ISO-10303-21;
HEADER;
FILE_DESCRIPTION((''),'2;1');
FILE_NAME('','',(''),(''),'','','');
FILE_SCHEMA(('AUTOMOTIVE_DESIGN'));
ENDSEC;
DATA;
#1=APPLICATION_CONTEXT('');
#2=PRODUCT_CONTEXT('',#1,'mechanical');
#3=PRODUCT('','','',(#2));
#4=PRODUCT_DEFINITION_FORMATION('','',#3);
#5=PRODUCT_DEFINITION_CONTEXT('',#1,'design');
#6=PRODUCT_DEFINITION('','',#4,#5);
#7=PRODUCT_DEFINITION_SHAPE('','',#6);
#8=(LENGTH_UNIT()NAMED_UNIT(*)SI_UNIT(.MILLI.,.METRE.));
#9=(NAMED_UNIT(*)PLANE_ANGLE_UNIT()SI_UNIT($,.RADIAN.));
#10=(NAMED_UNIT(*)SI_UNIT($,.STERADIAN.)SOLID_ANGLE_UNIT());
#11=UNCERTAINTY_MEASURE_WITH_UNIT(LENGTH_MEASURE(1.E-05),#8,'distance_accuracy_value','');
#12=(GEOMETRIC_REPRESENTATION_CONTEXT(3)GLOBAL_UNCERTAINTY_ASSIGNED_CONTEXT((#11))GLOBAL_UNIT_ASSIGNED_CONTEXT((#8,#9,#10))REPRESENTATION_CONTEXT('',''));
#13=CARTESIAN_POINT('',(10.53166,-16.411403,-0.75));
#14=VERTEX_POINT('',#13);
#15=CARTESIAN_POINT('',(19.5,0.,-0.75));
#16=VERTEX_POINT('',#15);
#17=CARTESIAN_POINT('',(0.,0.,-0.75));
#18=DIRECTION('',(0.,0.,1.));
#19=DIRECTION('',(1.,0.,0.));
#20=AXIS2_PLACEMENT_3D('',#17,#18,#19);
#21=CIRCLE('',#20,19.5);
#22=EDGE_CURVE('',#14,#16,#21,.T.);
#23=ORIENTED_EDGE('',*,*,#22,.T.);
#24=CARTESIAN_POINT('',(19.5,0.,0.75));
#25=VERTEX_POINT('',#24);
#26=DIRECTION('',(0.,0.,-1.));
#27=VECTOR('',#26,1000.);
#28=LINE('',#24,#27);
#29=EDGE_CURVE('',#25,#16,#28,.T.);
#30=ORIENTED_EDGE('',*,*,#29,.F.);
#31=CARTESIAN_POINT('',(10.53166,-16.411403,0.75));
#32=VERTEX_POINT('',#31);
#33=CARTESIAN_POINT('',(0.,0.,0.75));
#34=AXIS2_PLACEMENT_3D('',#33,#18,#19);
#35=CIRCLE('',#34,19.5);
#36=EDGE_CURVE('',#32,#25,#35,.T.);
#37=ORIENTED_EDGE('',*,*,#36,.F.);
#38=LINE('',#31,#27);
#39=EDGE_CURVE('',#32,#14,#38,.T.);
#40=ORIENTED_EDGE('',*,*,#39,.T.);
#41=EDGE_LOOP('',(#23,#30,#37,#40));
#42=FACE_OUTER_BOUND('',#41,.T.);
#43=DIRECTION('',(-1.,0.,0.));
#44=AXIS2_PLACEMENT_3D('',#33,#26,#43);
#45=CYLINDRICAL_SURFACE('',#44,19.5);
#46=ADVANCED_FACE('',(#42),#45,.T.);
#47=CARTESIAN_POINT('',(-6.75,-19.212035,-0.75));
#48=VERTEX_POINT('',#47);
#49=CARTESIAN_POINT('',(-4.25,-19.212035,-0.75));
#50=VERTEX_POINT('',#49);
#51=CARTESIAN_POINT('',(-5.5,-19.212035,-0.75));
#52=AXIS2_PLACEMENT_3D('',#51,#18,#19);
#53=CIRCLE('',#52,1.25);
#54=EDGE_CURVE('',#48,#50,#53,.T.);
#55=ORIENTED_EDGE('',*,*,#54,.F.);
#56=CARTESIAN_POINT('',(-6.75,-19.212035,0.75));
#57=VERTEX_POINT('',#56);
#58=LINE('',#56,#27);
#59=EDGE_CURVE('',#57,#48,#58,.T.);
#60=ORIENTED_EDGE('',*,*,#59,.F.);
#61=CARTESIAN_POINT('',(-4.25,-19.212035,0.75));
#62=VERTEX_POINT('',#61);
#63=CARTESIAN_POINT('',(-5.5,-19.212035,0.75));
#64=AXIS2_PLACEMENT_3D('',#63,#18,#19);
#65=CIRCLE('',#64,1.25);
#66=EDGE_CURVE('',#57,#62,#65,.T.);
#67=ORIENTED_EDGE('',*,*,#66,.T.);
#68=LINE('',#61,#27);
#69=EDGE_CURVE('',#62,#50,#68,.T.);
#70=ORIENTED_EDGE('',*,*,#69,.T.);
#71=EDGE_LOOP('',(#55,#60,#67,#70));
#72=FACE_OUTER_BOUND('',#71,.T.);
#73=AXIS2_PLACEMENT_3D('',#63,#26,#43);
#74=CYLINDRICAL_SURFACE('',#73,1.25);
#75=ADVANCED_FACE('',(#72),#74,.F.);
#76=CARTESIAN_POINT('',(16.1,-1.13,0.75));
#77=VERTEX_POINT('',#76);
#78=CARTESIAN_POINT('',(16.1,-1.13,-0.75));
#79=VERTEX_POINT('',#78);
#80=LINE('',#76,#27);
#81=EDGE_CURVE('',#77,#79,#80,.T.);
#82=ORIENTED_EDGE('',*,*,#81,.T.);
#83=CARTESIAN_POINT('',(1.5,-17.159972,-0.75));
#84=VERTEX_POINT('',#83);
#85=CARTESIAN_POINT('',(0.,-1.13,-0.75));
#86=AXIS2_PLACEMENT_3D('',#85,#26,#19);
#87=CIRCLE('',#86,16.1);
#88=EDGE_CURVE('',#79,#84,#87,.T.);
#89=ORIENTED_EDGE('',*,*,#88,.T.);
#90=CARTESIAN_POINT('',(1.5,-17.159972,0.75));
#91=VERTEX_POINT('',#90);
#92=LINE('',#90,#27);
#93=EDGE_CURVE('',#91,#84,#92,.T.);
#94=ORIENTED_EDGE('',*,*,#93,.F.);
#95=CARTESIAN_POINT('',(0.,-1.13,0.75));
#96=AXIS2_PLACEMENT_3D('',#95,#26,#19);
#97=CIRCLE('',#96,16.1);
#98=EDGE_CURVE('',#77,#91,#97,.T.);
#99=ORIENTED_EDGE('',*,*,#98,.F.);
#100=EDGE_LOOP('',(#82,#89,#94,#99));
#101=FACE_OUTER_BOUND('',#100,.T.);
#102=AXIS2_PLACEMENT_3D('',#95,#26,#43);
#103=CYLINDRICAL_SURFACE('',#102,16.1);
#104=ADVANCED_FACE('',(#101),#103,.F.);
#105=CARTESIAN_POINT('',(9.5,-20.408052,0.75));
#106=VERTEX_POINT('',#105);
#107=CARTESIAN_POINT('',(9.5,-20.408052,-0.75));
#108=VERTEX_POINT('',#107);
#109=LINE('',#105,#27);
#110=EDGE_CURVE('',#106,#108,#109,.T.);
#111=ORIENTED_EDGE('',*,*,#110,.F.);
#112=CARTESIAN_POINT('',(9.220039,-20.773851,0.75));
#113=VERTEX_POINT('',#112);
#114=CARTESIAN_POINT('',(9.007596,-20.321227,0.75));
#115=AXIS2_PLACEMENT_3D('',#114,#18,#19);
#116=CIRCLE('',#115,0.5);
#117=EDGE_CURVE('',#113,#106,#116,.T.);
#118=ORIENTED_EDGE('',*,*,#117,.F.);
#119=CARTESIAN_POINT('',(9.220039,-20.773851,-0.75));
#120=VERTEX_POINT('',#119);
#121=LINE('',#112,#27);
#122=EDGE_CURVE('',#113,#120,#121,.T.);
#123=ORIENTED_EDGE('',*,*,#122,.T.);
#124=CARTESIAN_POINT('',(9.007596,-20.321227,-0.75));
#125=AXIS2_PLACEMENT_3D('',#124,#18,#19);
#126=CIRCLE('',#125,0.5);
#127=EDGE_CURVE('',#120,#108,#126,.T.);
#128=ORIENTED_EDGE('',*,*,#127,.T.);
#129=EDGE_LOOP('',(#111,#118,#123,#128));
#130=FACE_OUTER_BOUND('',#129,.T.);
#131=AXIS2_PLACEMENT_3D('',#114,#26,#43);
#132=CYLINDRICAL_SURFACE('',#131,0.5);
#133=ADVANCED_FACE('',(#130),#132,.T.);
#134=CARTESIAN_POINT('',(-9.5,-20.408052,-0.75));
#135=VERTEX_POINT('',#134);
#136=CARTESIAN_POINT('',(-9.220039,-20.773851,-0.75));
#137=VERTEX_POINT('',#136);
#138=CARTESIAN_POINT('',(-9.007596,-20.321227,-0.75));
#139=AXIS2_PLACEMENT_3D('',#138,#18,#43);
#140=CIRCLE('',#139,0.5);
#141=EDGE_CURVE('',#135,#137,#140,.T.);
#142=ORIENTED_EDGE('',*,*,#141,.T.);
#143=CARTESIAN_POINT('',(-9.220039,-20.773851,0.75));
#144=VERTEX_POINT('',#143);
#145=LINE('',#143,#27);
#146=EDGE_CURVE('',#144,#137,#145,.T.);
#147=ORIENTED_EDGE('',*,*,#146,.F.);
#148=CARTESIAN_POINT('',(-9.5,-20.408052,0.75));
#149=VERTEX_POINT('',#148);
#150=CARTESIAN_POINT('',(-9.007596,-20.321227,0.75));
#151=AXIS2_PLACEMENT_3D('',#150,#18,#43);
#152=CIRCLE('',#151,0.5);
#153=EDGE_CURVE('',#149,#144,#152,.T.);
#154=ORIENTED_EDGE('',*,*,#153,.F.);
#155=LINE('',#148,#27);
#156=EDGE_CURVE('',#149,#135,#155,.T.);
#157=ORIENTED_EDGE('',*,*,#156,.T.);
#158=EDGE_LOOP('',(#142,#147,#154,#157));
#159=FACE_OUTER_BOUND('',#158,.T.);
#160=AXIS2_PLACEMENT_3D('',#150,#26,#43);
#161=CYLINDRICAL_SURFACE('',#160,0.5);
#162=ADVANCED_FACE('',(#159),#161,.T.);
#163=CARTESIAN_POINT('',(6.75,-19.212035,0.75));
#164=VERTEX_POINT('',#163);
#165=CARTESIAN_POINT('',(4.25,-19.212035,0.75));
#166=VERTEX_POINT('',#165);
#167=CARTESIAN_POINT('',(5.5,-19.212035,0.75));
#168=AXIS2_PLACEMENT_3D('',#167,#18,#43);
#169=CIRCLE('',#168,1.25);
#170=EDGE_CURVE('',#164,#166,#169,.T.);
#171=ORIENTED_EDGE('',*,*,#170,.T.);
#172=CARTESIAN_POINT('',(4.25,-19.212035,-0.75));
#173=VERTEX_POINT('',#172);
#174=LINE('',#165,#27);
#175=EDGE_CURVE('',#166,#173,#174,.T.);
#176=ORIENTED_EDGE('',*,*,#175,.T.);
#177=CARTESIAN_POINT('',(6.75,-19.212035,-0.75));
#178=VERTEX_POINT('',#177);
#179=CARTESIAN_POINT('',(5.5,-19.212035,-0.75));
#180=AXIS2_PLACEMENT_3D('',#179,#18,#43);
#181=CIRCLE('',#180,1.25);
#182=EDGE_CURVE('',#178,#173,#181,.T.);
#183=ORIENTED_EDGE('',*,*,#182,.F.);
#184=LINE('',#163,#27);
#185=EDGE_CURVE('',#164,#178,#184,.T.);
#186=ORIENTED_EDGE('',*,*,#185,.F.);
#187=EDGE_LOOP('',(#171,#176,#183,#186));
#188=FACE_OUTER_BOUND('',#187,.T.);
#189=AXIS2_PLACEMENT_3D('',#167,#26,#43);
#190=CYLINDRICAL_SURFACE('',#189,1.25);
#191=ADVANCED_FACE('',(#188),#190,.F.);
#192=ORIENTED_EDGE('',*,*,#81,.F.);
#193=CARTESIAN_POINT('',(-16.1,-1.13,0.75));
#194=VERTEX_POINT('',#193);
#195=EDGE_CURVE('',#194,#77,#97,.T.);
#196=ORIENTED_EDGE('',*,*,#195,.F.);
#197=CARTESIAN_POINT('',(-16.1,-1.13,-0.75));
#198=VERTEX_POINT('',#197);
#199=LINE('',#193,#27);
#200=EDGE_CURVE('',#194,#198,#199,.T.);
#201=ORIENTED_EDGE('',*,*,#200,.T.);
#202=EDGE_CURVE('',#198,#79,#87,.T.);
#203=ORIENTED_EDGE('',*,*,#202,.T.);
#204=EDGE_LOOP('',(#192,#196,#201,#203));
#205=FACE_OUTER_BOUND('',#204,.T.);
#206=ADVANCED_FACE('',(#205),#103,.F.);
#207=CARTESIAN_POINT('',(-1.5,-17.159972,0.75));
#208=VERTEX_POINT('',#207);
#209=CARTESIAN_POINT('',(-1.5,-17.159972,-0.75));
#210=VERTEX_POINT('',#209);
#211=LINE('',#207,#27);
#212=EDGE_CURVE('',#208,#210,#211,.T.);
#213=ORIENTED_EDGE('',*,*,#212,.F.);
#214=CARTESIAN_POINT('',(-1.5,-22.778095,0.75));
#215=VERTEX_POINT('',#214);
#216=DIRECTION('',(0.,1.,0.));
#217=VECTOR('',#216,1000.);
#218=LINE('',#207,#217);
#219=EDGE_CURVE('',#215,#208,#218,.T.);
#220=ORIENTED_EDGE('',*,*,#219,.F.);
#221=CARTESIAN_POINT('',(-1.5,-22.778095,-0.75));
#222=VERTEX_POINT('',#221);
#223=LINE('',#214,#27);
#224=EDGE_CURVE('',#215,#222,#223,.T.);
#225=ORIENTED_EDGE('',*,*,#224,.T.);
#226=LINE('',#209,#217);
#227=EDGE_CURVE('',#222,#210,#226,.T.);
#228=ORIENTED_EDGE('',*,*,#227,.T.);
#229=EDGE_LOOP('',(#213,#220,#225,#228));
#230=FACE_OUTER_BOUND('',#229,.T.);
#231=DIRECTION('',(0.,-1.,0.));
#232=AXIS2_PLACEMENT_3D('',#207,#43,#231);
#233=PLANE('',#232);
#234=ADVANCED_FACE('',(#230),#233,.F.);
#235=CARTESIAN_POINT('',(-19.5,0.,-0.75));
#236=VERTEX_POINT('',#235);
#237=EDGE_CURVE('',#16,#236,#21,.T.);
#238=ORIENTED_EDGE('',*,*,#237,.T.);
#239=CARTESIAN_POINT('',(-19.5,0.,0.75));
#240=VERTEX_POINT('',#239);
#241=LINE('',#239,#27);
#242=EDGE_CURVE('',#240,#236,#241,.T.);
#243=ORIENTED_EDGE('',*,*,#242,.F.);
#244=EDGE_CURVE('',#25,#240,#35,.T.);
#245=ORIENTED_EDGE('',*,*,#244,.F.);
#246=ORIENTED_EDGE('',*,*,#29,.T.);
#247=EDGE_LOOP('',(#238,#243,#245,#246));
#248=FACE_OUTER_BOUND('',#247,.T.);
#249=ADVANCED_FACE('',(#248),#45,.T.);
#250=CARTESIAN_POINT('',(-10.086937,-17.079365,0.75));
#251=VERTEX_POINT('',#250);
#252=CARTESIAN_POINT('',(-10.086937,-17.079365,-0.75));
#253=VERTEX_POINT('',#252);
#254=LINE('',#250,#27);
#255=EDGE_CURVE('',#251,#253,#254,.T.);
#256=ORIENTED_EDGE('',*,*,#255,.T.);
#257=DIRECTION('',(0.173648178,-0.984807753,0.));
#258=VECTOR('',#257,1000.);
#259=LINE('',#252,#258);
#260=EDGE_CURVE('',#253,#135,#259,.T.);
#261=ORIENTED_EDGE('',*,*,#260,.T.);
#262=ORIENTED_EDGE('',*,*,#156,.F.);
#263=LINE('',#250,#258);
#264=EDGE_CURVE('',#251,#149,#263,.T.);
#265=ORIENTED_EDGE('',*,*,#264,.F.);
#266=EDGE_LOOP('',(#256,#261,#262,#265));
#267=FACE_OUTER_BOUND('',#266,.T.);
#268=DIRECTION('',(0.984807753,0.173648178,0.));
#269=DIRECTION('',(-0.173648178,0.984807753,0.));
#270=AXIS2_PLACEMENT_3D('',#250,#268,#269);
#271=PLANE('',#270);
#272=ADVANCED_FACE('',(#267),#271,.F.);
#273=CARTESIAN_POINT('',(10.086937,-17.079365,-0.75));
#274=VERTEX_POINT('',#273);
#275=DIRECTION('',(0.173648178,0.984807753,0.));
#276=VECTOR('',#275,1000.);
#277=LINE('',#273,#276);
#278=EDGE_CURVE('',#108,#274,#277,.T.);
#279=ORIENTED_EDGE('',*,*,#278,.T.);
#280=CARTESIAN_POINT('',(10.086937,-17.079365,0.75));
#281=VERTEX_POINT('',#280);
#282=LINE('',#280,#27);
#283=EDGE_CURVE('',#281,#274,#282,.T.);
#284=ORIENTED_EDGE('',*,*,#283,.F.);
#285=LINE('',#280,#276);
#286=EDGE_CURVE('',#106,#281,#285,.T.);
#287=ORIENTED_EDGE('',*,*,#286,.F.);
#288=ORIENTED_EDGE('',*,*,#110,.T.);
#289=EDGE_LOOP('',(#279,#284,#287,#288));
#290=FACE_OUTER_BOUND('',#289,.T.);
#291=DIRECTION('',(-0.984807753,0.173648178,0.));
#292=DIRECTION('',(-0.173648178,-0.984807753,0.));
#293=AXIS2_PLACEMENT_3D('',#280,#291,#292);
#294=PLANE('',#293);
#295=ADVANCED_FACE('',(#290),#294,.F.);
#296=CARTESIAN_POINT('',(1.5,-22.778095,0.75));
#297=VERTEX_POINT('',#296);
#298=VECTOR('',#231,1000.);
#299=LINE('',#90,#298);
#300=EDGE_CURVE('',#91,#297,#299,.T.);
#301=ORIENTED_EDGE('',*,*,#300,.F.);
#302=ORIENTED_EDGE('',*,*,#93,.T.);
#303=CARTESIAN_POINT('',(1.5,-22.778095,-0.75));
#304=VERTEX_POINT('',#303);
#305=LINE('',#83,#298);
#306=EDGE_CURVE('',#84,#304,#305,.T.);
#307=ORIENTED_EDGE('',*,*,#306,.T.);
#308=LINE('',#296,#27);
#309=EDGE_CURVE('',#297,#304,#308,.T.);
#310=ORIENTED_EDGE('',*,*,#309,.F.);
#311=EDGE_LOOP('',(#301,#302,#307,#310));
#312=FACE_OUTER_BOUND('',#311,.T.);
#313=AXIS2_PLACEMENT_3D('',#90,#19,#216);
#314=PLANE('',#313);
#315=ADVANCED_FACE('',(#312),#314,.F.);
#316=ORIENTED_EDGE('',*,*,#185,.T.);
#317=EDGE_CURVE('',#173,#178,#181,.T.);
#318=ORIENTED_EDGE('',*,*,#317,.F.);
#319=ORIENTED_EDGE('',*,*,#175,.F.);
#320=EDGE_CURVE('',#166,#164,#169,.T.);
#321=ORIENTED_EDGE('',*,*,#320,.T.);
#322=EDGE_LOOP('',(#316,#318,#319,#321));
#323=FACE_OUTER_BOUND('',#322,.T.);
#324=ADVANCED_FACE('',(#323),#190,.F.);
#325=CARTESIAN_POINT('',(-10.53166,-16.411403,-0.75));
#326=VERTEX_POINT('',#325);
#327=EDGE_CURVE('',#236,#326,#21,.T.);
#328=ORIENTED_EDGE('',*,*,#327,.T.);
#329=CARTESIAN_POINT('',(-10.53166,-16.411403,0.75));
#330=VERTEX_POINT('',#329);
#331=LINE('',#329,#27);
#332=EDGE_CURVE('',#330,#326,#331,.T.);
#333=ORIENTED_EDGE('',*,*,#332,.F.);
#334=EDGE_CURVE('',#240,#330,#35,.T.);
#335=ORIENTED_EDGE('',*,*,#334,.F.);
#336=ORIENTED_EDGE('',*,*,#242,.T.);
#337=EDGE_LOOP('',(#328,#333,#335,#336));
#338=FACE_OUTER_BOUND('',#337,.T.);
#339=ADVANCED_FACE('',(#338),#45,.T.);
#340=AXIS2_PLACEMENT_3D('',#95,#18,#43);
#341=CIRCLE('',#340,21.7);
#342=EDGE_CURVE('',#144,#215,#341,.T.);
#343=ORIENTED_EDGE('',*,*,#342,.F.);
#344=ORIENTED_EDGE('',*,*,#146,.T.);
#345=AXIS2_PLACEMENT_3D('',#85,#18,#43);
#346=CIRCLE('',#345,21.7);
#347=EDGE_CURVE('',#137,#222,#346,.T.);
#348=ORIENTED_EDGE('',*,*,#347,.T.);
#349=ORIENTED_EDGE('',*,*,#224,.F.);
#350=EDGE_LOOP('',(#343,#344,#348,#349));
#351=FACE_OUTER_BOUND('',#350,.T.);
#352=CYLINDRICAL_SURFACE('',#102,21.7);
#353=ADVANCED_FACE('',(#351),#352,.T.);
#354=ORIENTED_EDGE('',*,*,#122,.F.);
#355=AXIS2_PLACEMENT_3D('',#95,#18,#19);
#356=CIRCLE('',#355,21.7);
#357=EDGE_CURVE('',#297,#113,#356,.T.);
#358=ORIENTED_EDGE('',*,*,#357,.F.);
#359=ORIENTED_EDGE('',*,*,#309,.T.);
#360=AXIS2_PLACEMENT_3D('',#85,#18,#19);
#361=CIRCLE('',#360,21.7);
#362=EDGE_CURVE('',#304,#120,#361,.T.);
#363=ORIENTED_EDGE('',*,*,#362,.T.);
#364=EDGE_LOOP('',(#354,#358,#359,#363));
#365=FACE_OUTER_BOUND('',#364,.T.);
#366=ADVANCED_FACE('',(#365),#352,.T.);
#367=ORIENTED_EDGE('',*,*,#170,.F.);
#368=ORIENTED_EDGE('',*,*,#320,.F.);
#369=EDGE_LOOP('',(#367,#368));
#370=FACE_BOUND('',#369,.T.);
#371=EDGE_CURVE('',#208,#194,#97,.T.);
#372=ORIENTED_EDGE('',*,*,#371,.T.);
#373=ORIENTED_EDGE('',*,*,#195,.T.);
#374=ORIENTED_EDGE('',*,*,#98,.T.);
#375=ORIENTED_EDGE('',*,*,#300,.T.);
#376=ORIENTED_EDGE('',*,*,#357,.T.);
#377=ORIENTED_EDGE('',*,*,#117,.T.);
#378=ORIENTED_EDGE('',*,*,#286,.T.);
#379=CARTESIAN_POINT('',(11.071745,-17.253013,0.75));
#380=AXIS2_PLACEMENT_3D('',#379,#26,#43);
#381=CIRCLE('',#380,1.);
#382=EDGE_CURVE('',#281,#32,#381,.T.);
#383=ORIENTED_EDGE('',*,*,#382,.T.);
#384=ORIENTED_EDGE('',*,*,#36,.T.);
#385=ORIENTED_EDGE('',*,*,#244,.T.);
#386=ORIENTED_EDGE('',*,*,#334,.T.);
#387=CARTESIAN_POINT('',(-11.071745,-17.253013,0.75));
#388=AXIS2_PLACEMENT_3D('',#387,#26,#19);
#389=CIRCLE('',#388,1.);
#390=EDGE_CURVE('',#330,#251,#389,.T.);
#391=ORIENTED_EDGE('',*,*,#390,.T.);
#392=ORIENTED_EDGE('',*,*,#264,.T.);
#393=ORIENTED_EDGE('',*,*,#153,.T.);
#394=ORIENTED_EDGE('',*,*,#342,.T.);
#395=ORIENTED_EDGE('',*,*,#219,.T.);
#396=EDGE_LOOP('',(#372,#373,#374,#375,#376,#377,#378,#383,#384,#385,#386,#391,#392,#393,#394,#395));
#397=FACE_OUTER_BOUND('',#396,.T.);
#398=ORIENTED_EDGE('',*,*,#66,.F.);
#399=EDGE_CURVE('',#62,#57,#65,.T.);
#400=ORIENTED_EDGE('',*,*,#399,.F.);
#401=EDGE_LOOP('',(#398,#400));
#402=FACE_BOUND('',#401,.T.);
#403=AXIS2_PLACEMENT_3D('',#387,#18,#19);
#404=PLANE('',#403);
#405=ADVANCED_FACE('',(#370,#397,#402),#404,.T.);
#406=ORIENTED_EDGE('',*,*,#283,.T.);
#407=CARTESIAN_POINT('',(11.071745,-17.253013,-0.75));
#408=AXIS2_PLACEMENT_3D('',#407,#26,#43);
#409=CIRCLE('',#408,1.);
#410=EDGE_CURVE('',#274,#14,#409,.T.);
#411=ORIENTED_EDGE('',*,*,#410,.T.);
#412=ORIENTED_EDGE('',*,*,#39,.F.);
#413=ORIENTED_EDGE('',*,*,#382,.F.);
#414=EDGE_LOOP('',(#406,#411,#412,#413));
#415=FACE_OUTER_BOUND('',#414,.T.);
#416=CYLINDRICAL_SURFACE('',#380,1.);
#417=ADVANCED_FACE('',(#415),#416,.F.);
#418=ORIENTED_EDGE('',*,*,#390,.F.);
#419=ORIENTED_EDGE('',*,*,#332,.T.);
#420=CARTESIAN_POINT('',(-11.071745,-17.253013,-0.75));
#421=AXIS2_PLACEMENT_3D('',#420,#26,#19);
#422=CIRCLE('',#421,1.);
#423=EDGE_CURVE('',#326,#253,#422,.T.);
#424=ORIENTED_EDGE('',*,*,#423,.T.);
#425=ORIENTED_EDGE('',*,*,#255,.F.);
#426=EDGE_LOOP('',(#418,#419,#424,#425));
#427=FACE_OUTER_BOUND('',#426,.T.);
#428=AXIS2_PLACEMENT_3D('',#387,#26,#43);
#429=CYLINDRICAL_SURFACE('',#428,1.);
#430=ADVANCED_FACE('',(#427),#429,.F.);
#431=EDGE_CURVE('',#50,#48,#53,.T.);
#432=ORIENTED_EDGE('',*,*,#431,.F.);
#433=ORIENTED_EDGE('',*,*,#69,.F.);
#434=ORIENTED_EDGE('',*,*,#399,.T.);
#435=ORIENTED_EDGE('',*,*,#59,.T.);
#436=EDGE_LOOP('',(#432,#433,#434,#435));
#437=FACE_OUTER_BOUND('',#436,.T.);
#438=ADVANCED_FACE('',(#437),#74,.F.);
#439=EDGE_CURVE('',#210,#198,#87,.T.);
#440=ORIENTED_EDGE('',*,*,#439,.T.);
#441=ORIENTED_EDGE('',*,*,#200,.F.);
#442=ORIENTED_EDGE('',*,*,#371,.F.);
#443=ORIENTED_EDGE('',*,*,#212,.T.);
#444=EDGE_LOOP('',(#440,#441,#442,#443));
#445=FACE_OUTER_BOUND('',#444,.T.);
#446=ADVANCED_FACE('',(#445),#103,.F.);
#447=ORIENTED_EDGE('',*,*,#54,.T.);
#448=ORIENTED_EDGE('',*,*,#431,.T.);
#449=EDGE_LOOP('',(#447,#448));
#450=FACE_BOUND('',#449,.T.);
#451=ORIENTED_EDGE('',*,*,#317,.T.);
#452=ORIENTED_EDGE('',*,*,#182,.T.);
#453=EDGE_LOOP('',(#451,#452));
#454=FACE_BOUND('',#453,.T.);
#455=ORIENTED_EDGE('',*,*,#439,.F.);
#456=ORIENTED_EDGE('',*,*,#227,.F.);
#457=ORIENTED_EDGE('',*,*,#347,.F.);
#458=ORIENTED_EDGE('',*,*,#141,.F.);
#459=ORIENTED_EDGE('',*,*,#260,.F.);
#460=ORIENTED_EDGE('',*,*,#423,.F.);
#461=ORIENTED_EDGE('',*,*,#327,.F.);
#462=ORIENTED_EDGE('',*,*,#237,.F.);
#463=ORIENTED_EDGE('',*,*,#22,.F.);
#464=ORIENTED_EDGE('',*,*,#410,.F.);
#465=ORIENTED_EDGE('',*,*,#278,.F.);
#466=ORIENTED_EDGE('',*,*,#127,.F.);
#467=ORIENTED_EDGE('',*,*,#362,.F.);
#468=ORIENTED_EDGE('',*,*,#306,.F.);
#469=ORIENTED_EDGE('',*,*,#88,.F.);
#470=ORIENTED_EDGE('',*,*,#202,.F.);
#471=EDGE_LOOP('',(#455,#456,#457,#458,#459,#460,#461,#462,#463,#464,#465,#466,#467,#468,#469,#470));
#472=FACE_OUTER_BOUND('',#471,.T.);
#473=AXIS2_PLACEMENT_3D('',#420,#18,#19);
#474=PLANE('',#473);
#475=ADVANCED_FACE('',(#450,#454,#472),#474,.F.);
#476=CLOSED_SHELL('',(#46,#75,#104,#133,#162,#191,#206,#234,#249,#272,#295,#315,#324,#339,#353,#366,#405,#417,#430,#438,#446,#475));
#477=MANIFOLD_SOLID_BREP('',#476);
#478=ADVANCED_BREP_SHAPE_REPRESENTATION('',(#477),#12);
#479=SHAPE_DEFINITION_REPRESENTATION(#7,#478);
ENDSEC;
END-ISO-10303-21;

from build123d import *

# Parameters (mm, degrees)
BASE_EXTRUDE_DEPTH      = 0.75
BASE_EXTRUDE_DEPTH_BACK = 0.75
SKETCH1_R               = 1.25


with BuildPart() as part:
    # Sketch1 → Base-Extrude (new, two sides: drawn at the far end of the back side and taken through both)
    with BuildSketch(Plane.XY.offset(-BASE_EXTRUDE_DEPTH_BACK)):
        with BuildLine():
            Line((-1.5, -17.159971928), (-1.5, -22.778094604))
            ThreePointArc((-1.5, -22.778094604), (-5.452894614, -22.133712537), (-9.220039428, -20.773850767))
            ThreePointArc((-9.220039428, -20.773850767), (-9.404653614, -20.625111252), (-9.5, -20.408051566))
            Line((-9.5, -20.408051566), (-10.086937259, -17.079364962))
            ThreePointArc((-10.086937259, -17.079364962), (-10.239358111, -16.698818185), (-10.531659889, -16.411402743))
            ThreePointArc((-10.531659889, -16.411402743), (0, 19.5), (10.531659889, -16.411402743))
            ThreePointArc((10.531659889, -16.411402743), (10.239358111, -16.698818185), (10.086937259, -17.079364962))
            Line((10.086937259, -17.079364962), (9.5, -20.408051566))
            ThreePointArc((9.5, -20.408051566), (9.404653614, -20.625111252), (9.220039428, -20.773850767))
            ThreePointArc((9.220039428, -20.773850767), (5.452894614, -22.133712537), (1.5, -22.778094604))
            Line((1.5, -22.778094604), (1.5, -17.159971928))
            ThreePointArc((1.5, -17.159971928), (0, 14.97), (-1.5, -17.159971928))
        make_face()
        with Locations((-5.5, -19.212035284)):
            Circle(SKETCH1_R, mode=Mode.SUBTRACT)
        with Locations(Location((5.5, -19.212035284, 0), (0, 0, 180))):
            Circle(SKETCH1_R, mode=Mode.SUBTRACT)
    extrude(amount=BASE_EXTRUDE_DEPTH + BASE_EXTRUDE_DEPTH_BACK)


solid = part.part
